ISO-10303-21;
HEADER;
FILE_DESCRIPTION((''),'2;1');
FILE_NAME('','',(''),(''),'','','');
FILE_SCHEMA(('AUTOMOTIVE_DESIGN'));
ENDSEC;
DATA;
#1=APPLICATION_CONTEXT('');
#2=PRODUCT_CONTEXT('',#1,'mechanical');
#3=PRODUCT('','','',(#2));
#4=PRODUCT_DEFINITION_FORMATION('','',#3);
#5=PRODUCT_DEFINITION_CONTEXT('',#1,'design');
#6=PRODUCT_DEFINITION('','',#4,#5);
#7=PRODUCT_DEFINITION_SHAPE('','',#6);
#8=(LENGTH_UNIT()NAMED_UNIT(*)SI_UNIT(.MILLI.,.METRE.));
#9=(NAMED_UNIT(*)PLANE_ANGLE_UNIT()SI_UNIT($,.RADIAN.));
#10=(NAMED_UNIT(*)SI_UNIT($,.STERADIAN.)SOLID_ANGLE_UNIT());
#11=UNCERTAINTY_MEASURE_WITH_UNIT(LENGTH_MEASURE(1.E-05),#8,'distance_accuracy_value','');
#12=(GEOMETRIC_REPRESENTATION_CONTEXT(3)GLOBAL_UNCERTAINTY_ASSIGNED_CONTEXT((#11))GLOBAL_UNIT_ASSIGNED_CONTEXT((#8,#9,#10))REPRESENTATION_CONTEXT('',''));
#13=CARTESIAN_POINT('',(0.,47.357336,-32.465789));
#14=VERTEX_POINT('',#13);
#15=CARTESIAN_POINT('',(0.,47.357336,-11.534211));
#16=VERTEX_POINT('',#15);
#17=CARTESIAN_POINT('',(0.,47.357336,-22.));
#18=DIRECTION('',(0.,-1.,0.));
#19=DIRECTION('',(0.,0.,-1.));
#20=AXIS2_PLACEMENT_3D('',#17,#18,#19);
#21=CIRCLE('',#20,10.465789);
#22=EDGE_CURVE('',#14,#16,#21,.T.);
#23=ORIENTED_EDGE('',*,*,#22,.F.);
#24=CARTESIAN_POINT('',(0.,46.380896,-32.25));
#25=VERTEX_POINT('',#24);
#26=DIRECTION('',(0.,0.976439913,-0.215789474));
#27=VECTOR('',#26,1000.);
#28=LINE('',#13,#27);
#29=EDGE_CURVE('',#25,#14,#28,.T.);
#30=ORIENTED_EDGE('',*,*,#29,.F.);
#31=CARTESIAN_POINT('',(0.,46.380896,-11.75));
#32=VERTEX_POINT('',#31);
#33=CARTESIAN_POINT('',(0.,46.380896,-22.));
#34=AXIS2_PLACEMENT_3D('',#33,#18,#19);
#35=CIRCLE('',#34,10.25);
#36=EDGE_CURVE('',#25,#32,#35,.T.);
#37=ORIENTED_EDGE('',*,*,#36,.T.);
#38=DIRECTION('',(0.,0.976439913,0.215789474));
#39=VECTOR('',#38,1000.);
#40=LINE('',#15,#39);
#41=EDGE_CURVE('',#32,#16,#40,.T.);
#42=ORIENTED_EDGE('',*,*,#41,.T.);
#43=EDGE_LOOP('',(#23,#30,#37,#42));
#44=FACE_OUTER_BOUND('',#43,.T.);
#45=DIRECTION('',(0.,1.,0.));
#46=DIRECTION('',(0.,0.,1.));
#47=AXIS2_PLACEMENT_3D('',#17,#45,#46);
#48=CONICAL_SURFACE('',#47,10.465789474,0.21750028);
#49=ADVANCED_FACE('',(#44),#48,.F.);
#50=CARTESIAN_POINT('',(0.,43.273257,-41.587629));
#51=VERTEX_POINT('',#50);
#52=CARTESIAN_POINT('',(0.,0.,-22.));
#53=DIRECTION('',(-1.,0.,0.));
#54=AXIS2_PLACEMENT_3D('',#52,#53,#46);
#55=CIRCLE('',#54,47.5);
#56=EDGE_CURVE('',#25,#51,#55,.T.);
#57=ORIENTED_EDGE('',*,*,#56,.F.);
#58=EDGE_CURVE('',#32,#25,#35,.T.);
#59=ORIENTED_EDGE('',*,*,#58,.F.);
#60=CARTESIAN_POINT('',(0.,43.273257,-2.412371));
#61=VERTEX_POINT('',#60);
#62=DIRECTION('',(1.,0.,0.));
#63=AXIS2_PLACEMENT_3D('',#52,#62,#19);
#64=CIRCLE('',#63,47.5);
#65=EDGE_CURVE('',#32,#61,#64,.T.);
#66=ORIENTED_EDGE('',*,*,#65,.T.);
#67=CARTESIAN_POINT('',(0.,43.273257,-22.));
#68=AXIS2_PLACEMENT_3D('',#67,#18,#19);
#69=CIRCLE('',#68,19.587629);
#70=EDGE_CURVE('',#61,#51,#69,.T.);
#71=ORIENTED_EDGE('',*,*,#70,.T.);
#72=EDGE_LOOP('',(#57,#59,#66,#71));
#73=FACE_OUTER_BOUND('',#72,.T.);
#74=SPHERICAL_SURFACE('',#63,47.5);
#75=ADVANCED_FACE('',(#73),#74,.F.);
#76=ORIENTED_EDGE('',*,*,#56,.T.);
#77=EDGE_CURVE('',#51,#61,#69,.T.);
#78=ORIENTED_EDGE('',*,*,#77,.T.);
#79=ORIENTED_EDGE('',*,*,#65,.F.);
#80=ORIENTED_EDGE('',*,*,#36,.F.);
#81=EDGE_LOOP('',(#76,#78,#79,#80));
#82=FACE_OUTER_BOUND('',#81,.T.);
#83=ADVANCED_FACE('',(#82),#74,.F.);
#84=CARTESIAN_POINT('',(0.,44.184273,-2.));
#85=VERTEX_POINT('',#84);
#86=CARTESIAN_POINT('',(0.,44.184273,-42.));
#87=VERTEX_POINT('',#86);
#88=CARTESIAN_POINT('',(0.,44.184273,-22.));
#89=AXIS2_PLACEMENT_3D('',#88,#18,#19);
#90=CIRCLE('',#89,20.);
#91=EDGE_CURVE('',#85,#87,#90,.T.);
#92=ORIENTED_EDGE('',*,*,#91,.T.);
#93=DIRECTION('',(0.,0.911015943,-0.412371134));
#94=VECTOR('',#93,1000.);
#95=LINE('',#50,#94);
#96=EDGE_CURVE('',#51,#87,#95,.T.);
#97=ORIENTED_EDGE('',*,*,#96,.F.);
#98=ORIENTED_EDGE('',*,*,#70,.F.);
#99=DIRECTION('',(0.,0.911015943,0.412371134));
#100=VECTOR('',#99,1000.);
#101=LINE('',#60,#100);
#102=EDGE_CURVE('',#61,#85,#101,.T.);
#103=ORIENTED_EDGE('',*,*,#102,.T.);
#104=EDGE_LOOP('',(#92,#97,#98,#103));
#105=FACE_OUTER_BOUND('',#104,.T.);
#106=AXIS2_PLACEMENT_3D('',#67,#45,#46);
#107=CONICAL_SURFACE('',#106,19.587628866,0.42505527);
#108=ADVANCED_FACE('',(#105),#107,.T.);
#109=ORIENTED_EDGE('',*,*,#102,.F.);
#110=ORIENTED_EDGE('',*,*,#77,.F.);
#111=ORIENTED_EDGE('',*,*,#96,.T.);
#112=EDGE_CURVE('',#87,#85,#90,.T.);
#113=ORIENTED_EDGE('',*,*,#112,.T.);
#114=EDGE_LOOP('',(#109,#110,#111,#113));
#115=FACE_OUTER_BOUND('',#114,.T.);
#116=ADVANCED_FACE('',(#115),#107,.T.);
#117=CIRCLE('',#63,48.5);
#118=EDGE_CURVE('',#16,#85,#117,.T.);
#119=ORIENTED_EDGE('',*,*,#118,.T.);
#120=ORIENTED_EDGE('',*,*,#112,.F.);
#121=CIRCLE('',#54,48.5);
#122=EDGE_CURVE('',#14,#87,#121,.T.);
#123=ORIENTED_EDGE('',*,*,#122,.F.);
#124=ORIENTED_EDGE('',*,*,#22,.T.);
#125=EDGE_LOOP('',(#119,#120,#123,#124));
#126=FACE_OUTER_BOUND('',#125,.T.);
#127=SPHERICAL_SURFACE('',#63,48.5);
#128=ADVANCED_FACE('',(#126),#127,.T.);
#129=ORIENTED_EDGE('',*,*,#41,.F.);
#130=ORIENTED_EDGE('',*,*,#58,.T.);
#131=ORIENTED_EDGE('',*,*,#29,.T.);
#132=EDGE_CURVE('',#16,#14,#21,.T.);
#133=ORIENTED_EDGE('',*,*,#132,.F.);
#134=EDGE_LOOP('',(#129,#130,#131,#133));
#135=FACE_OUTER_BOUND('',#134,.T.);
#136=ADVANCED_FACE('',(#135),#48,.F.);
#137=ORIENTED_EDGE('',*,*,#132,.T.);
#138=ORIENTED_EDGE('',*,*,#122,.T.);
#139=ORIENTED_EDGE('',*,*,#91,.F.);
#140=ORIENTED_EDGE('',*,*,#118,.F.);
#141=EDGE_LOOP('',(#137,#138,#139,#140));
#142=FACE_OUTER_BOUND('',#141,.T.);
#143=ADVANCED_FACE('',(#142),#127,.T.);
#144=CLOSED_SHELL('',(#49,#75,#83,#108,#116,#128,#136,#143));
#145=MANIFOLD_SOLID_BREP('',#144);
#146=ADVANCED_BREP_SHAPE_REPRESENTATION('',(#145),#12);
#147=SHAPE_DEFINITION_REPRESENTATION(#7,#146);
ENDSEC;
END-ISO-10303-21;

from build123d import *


with BuildPart() as part:
    # Sketch1 → Revolve1 (revolve)
    with BuildSketch(Plane(origin=(0, 0, 0), x_dir=(0, 0, -1), z_dir=(1, 0, 0))):
        with BuildLine():
            Line((32.25, 46.380895852), (32.465789474, 47.357335764))
            ThreePointArc((32.465789474, 47.357335764), (37.31529182, 46.018385852), (42, 44.18427322))
            Line((42, 44.18427322), (41.587628866, 43.273257278))
            ThreePointArc((41.587628866, 43.273257278), (36.999512608, 45.069553154), (32.25, 46.380895852))
        make_face()
    revolve(axis=Axis((0, 0, -22), (0, 1, 0)))


solid = part.part
